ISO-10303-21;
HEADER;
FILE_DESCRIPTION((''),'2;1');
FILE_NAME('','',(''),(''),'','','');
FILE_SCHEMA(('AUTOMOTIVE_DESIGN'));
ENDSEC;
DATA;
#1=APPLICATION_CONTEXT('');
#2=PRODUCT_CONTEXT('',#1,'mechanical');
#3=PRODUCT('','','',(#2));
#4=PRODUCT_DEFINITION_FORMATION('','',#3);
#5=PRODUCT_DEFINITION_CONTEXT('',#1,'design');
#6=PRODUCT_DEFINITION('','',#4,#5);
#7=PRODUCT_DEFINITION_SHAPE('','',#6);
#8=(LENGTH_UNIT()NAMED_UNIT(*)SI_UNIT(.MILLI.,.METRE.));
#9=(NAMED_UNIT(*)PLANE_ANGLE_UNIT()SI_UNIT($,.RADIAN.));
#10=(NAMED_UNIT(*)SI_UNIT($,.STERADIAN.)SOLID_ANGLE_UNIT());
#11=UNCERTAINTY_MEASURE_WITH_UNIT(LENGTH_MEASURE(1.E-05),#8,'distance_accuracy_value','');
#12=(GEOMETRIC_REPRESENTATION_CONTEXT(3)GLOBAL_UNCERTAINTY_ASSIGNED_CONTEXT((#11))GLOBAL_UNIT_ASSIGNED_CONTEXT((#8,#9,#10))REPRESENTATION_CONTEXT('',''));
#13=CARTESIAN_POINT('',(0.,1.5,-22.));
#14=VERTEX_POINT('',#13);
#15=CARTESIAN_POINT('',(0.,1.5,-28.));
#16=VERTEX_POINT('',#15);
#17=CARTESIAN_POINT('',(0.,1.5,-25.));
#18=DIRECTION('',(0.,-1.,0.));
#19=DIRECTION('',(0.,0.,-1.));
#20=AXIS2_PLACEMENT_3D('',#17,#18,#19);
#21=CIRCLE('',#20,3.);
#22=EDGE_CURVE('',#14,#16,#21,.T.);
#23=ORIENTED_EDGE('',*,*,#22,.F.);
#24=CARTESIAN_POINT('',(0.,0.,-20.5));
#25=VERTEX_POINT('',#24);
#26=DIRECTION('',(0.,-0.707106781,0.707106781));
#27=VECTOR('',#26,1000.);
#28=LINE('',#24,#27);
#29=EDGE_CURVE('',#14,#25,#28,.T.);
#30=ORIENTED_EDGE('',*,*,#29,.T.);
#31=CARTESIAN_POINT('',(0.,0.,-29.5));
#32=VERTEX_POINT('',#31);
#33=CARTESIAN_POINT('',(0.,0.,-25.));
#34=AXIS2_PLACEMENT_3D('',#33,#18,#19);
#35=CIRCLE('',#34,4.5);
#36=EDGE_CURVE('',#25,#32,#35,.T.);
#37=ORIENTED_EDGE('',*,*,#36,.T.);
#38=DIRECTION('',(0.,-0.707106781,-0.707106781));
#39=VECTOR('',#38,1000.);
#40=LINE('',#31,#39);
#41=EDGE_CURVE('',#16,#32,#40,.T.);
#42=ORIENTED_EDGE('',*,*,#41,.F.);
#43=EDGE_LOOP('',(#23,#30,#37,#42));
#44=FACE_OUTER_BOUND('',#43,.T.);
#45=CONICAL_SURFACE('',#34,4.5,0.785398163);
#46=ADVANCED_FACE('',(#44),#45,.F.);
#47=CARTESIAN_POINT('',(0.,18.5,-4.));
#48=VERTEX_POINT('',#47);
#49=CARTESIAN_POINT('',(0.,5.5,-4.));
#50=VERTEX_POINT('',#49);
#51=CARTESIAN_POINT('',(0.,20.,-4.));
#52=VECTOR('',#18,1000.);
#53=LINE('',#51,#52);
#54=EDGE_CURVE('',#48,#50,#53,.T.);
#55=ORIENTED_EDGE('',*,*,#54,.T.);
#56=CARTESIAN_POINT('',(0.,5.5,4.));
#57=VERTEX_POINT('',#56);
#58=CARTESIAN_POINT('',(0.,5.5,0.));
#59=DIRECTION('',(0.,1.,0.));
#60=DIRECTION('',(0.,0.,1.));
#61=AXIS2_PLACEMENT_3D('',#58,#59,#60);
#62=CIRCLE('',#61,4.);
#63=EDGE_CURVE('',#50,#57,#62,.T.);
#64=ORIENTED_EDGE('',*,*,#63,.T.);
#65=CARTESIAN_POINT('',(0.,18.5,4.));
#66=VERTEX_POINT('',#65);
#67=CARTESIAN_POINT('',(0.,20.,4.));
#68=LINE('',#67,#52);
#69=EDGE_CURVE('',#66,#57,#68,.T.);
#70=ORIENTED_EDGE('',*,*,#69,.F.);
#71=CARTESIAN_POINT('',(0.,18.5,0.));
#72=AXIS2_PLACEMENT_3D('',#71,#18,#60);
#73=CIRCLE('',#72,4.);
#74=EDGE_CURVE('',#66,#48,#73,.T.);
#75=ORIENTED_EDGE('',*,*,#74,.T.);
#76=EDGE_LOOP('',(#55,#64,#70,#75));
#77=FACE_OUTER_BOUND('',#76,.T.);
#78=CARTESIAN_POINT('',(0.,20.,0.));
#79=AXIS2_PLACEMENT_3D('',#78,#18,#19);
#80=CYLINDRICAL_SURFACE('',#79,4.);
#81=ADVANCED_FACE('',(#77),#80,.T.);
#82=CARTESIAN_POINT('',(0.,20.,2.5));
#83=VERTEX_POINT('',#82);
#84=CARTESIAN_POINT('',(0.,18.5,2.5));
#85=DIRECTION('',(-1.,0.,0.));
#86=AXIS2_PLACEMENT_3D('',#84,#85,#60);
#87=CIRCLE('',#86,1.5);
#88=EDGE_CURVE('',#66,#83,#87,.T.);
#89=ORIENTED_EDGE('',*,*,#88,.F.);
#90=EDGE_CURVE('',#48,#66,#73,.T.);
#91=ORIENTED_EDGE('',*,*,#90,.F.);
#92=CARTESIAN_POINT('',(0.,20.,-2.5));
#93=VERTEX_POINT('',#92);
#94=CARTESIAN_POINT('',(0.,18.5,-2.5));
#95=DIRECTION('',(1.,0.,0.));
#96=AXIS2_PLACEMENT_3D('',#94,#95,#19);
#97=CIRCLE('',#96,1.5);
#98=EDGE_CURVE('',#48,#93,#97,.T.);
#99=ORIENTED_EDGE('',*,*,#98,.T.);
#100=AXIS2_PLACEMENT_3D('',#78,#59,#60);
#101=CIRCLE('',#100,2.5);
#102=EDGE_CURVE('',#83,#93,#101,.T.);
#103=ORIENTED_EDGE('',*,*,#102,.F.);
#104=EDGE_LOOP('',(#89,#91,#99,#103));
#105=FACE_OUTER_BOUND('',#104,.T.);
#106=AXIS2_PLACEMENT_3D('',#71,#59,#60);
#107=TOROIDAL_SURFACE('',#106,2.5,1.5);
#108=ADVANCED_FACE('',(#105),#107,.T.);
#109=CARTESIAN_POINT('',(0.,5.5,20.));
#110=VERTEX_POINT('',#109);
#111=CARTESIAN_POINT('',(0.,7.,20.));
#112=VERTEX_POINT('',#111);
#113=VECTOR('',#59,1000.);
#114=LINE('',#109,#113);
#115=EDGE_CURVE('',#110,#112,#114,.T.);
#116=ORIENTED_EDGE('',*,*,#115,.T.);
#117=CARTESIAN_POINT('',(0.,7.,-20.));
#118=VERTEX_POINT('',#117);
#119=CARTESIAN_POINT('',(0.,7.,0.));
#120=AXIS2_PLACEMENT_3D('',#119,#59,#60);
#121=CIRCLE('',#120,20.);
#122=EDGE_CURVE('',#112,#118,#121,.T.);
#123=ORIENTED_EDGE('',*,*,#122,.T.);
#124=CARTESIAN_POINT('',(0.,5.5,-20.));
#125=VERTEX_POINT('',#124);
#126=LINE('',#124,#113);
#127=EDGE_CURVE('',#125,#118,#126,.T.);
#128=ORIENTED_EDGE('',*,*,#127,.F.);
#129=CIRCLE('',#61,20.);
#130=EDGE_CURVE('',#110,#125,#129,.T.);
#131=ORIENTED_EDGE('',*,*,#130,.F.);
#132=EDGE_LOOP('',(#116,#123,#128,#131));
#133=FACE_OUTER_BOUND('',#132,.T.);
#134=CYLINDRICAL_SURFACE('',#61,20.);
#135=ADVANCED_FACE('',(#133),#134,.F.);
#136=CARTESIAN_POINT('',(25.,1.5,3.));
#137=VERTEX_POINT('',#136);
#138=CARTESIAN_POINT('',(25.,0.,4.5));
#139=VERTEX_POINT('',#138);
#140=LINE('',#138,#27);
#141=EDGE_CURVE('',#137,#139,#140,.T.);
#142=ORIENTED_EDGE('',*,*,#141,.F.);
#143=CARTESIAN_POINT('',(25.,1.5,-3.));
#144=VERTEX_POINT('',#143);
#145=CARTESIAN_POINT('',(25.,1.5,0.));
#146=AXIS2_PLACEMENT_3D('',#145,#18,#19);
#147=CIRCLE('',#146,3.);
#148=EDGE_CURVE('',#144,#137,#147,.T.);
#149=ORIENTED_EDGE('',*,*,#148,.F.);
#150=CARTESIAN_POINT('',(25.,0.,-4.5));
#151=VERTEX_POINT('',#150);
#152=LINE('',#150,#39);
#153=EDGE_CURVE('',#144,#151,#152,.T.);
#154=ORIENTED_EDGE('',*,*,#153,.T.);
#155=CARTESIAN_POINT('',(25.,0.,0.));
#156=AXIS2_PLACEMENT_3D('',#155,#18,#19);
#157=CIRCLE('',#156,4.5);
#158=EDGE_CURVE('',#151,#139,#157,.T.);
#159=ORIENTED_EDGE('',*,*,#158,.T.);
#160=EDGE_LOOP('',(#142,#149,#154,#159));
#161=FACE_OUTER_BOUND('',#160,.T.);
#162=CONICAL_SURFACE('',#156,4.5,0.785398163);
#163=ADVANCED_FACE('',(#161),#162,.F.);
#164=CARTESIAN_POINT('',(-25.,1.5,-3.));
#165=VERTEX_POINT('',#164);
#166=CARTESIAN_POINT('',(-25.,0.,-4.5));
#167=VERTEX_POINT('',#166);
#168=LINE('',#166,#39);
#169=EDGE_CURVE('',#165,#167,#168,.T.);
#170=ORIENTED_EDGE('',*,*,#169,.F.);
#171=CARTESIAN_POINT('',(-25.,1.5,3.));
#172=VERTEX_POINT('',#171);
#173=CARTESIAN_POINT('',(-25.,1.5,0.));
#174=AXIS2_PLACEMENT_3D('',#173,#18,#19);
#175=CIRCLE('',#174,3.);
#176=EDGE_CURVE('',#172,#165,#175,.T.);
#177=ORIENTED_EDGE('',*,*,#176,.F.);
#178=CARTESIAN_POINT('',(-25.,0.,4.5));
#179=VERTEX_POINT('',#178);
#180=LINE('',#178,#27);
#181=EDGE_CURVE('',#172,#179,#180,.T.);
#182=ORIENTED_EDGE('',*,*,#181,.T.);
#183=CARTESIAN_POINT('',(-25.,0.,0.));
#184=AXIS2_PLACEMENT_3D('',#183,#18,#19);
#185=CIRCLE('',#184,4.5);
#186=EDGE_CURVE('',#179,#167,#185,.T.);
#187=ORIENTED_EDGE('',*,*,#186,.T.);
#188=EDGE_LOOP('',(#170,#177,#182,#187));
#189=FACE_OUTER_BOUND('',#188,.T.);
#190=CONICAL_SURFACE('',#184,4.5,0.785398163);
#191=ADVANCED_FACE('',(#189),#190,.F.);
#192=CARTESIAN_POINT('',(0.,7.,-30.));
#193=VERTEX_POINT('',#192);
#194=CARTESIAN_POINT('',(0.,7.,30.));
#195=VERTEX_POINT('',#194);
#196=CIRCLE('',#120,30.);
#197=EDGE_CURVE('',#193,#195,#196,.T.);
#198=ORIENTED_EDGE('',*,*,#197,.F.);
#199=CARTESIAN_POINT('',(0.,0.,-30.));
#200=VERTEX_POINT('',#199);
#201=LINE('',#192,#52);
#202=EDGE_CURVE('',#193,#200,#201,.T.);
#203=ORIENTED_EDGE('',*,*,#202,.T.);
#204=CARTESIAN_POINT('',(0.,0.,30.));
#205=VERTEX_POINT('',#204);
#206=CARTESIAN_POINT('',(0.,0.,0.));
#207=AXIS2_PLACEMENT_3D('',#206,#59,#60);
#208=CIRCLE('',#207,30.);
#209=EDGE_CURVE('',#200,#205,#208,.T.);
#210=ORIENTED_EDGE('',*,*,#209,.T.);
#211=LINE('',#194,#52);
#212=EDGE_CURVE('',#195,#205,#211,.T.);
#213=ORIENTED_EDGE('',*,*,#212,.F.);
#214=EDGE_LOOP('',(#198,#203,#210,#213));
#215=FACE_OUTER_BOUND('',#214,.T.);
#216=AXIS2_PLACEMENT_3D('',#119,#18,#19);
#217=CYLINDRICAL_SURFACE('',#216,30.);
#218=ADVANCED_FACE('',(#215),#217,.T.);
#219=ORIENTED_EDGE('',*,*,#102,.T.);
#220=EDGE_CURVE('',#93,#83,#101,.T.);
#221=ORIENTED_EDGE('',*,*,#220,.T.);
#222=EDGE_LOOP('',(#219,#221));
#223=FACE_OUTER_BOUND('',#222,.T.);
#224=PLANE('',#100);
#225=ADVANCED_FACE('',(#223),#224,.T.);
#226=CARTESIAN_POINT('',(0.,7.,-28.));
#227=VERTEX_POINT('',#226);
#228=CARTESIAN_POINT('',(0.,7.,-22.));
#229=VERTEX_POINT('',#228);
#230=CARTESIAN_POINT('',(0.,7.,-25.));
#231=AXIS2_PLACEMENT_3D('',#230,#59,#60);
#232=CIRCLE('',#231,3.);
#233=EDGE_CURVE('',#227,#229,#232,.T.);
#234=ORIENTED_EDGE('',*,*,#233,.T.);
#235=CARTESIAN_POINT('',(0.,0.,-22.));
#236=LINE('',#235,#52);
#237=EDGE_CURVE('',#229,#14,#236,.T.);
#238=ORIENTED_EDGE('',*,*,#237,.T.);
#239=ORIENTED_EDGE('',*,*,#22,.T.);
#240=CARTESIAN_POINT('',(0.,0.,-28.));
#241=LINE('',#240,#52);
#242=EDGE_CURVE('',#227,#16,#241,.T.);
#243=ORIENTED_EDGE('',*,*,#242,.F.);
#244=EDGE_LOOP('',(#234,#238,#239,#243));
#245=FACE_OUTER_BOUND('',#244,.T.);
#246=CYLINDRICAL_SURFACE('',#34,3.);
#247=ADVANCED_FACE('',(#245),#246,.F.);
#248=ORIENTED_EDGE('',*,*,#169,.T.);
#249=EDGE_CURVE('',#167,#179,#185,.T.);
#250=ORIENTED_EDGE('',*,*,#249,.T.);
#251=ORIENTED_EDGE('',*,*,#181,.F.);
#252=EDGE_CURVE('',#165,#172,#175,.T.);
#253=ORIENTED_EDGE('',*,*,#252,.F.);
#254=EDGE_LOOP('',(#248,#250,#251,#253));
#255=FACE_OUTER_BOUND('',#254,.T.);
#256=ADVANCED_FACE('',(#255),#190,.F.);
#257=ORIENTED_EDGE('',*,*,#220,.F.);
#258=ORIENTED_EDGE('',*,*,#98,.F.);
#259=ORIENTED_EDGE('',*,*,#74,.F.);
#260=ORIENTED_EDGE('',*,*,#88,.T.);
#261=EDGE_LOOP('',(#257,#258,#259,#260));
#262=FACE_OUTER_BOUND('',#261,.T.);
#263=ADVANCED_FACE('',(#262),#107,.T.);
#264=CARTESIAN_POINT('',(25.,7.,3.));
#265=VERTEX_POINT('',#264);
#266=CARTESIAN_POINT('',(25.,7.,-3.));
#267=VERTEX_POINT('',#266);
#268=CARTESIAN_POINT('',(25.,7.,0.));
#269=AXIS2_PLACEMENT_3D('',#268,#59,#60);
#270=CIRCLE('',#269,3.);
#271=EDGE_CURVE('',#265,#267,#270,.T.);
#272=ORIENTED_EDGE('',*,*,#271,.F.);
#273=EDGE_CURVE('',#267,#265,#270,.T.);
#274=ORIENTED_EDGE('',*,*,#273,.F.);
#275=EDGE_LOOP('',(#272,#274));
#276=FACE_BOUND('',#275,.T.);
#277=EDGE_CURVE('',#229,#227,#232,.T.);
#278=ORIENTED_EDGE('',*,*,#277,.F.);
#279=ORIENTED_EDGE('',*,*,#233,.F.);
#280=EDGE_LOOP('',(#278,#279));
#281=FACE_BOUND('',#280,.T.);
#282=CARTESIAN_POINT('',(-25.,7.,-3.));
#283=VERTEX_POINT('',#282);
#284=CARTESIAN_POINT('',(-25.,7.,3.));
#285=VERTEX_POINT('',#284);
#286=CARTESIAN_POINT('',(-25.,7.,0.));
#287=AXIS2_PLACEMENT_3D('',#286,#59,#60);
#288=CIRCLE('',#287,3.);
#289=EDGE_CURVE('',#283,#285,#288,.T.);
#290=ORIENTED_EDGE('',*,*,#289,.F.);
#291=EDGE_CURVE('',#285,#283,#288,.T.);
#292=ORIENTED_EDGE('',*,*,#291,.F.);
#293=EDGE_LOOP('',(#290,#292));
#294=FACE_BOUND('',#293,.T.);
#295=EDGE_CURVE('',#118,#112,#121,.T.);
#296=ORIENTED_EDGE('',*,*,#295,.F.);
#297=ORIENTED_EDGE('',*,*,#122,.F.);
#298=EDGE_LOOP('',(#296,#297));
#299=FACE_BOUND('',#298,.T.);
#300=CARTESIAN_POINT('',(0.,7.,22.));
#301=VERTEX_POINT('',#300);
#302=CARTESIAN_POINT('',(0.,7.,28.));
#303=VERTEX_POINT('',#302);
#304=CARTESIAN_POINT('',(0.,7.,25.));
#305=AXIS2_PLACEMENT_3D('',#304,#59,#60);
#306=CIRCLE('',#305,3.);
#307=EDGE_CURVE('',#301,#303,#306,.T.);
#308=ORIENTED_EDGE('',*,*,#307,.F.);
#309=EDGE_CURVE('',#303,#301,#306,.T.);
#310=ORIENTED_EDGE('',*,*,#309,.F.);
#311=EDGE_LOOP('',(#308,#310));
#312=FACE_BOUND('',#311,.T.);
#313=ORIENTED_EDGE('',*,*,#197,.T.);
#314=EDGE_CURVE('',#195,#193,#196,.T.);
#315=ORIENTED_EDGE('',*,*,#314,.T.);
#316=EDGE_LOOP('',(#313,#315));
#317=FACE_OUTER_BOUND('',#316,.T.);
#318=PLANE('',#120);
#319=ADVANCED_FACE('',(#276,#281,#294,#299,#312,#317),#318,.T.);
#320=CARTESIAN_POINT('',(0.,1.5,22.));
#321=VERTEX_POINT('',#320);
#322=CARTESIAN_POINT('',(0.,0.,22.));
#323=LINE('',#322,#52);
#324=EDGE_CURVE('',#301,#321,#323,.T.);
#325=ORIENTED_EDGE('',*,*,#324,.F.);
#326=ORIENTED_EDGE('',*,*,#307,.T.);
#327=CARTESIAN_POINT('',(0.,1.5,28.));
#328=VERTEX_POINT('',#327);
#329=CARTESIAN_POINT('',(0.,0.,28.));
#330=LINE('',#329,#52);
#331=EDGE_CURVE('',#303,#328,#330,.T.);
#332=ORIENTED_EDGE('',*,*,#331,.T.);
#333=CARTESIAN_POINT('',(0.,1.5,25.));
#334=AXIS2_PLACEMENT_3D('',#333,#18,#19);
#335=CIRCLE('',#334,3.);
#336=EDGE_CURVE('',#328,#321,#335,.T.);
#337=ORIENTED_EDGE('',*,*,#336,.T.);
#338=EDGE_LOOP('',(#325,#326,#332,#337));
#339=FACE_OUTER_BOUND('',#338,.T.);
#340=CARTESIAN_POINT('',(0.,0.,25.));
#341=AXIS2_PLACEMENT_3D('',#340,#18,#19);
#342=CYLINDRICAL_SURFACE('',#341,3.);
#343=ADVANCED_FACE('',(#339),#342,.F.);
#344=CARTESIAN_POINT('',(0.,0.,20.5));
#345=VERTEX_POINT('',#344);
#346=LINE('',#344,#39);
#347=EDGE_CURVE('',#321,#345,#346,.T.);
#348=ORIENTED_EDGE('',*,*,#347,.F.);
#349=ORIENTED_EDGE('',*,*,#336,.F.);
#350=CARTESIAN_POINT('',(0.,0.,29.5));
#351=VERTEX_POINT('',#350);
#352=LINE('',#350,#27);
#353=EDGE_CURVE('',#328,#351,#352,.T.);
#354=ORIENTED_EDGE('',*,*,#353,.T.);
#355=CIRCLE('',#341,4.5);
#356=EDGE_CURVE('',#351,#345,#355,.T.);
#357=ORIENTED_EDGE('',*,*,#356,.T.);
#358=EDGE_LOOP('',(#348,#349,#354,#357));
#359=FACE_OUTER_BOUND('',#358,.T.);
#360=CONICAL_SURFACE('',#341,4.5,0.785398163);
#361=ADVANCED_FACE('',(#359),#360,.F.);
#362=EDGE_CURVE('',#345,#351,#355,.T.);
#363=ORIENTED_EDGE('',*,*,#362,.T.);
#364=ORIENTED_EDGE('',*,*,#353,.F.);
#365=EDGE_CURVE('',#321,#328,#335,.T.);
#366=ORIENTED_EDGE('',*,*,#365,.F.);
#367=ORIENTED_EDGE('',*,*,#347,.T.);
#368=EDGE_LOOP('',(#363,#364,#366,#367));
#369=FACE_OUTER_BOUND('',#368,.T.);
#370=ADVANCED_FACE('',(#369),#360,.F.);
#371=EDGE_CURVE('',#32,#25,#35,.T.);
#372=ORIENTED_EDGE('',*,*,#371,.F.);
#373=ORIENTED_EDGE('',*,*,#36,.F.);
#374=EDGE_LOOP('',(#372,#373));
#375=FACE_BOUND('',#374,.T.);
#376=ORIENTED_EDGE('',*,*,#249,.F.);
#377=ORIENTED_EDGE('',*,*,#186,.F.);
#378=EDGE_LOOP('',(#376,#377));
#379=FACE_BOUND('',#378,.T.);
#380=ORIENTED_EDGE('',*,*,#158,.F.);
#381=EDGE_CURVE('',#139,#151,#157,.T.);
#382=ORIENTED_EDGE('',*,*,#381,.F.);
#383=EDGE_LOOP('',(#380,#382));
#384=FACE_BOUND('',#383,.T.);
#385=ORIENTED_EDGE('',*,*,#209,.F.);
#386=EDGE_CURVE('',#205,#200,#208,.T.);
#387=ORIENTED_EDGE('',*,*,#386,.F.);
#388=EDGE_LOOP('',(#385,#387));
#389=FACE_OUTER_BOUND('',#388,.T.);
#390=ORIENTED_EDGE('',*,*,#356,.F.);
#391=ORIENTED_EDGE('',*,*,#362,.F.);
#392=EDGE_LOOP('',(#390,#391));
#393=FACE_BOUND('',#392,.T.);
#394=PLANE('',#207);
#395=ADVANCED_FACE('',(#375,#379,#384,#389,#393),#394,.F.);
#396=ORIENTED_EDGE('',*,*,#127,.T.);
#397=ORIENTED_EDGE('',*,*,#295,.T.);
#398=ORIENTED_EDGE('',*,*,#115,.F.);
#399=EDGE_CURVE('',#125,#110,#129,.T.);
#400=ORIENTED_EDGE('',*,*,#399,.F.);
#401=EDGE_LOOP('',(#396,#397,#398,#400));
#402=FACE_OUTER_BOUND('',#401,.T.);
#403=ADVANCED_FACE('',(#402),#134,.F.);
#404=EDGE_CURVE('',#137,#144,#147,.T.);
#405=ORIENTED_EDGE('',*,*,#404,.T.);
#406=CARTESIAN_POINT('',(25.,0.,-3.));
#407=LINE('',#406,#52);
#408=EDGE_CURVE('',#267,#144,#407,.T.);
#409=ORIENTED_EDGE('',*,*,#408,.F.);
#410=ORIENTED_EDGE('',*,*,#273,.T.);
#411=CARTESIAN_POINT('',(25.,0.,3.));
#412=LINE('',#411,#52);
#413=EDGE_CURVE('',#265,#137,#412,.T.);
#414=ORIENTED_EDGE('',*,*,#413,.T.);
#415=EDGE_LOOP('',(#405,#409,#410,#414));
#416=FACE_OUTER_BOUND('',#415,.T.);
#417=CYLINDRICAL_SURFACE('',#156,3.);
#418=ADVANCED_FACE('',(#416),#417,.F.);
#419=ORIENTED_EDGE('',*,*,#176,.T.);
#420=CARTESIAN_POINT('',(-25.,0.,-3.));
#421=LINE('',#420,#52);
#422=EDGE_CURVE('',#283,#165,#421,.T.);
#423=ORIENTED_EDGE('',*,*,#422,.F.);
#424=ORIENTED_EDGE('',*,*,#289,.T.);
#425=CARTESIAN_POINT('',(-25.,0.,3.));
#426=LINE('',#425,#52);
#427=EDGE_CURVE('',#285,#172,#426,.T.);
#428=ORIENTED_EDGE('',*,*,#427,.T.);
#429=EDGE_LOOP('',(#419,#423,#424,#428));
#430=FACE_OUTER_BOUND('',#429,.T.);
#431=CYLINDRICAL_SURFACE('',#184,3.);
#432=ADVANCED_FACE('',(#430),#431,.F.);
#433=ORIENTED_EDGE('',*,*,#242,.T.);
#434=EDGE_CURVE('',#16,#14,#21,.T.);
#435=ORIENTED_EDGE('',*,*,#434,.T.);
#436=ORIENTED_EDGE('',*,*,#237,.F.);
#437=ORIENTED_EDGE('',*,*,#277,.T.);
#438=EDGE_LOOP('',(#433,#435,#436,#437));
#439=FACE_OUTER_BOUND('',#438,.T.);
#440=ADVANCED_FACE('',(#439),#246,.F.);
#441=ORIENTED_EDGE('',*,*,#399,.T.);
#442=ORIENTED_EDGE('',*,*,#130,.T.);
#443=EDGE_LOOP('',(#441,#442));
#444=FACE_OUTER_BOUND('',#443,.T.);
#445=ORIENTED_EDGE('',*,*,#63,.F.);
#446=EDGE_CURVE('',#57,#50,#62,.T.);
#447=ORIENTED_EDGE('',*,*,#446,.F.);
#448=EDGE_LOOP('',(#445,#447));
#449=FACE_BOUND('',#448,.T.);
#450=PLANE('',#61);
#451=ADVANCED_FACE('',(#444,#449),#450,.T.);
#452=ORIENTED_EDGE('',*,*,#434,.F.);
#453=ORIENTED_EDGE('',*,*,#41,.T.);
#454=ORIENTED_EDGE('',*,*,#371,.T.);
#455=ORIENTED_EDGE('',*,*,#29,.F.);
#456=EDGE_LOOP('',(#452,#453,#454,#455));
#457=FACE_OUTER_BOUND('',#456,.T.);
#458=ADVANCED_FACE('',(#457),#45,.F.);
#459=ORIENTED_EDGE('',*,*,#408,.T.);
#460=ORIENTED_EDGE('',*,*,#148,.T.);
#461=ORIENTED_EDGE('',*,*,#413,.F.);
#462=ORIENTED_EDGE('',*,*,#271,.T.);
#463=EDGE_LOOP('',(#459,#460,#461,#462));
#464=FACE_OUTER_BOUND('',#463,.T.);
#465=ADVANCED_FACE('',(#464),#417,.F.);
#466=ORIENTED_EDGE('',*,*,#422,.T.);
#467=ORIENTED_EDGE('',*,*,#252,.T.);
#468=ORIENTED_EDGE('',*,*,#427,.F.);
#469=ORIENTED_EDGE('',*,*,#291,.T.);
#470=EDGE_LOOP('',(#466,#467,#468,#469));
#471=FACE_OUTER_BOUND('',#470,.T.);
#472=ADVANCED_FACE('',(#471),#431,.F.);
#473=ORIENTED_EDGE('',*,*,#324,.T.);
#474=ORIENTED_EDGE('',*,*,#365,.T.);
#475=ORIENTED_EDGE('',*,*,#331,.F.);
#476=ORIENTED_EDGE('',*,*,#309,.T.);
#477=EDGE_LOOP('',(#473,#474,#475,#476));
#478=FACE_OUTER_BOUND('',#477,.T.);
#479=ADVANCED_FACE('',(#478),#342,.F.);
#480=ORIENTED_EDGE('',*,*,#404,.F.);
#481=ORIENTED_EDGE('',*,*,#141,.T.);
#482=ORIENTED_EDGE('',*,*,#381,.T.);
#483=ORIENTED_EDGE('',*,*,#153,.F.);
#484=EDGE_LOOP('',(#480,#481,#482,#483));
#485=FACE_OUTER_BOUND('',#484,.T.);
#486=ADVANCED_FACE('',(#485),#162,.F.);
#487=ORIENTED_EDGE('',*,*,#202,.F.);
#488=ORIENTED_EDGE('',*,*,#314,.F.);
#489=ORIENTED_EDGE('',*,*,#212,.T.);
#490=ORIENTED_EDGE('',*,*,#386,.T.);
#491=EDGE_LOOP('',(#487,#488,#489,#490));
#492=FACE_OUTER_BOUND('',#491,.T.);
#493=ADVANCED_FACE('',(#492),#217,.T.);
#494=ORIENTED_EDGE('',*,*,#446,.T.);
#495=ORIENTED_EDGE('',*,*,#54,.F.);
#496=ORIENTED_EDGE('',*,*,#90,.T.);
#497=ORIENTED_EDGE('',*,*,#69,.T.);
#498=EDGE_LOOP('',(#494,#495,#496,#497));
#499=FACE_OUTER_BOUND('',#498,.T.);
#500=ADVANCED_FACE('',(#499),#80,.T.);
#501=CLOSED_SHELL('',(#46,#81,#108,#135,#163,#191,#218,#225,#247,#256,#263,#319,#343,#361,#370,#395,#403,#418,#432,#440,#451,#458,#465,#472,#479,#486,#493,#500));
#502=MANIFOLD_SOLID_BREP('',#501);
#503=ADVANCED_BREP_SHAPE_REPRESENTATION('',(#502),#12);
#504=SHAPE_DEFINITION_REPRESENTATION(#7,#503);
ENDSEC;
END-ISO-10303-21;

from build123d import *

# Parameters (mm, degrees)
SKETCH1_R           = 30
BOSS_EXTRUDE1_DEPTH = 7
SKETCH2_R           = 4
BOSS_EXTRUDE2_DEPTH = 13
CUT_EXTRUDE1_START  = -1.5
SKETCH3_R           = 20
SKETCH3_R_2         = 4
CUT_EXTRUDE1_DEPTH  = 1.5
HOLE1_D             = 6
HOLE1_CSINK_D       = 9
HOLE1_CSINK_ANGLE   = 90
FILLET1_R           = 1.5


with BuildPart() as part:
    # Sketch1 → Boss-Extrude1 (new body)
    with BuildSketch(Plane(origin=(0, 0, 0), x_dir=(1, 0, 0), z_dir=(0, 1, 0))):
        with Locations(Location((0, 0, 0), (0, 0, 270))):
            Circle(SKETCH1_R)
    extrude(amount=BOSS_EXTRUDE1_DEPTH)

    # Sketch2 → Boss-Extrude2 (add)
    with BuildSketch(Plane(origin=(0, 7, 0), x_dir=(1, 0, 0), z_dir=(0, 1, 0))):
        with Locations(Location((0, 0, 0), (0, 0, 90))):
            Circle(SKETCH2_R)
    extrude(amount=BOSS_EXTRUDE2_DEPTH)

    # Sketch3 → Cut-Extrude1 (cut)
    with BuildSketch(Plane(origin=(0, 7, 0), x_dir=(1, 0, 0), z_dir=(0, 1, 0)).offset(CUT_EXTRUDE1_START)):
        with Locations(Location((0, 0, 0), (0, 0, 270))):
            Circle(SKETCH3_R)
        with Locations(Location((0, 0, 0), (0, 0, 90))):
            Circle(SKETCH3_R_2, mode=Mode.SUBTRACT)
    extrude(amount=CUT_EXTRUDE1_DEPTH, mode=Mode.SUBTRACT)

    # Hole1 (through all)
    with Locations(Plane(origin=(0, 0, 0), x_dir=(-1, 0, 0), z_dir=(0, -1, 0))):
        with Locations((-25, 0), (0, 25), (25, 0), (0, -25)):
            CounterSinkHole(HOLE1_D / 2, HOLE1_CSINK_D / 2, counter_sink_angle=HOLE1_CSINK_ANGLE)

    # Fillet1
    fillet1_edges = [part.edges().sort_by_distance(p)[0] for p in [
        (0, 20, 4),
    ]]
    fillet(fillet1_edges, radius=FILLET1_R)


solid = part.part
